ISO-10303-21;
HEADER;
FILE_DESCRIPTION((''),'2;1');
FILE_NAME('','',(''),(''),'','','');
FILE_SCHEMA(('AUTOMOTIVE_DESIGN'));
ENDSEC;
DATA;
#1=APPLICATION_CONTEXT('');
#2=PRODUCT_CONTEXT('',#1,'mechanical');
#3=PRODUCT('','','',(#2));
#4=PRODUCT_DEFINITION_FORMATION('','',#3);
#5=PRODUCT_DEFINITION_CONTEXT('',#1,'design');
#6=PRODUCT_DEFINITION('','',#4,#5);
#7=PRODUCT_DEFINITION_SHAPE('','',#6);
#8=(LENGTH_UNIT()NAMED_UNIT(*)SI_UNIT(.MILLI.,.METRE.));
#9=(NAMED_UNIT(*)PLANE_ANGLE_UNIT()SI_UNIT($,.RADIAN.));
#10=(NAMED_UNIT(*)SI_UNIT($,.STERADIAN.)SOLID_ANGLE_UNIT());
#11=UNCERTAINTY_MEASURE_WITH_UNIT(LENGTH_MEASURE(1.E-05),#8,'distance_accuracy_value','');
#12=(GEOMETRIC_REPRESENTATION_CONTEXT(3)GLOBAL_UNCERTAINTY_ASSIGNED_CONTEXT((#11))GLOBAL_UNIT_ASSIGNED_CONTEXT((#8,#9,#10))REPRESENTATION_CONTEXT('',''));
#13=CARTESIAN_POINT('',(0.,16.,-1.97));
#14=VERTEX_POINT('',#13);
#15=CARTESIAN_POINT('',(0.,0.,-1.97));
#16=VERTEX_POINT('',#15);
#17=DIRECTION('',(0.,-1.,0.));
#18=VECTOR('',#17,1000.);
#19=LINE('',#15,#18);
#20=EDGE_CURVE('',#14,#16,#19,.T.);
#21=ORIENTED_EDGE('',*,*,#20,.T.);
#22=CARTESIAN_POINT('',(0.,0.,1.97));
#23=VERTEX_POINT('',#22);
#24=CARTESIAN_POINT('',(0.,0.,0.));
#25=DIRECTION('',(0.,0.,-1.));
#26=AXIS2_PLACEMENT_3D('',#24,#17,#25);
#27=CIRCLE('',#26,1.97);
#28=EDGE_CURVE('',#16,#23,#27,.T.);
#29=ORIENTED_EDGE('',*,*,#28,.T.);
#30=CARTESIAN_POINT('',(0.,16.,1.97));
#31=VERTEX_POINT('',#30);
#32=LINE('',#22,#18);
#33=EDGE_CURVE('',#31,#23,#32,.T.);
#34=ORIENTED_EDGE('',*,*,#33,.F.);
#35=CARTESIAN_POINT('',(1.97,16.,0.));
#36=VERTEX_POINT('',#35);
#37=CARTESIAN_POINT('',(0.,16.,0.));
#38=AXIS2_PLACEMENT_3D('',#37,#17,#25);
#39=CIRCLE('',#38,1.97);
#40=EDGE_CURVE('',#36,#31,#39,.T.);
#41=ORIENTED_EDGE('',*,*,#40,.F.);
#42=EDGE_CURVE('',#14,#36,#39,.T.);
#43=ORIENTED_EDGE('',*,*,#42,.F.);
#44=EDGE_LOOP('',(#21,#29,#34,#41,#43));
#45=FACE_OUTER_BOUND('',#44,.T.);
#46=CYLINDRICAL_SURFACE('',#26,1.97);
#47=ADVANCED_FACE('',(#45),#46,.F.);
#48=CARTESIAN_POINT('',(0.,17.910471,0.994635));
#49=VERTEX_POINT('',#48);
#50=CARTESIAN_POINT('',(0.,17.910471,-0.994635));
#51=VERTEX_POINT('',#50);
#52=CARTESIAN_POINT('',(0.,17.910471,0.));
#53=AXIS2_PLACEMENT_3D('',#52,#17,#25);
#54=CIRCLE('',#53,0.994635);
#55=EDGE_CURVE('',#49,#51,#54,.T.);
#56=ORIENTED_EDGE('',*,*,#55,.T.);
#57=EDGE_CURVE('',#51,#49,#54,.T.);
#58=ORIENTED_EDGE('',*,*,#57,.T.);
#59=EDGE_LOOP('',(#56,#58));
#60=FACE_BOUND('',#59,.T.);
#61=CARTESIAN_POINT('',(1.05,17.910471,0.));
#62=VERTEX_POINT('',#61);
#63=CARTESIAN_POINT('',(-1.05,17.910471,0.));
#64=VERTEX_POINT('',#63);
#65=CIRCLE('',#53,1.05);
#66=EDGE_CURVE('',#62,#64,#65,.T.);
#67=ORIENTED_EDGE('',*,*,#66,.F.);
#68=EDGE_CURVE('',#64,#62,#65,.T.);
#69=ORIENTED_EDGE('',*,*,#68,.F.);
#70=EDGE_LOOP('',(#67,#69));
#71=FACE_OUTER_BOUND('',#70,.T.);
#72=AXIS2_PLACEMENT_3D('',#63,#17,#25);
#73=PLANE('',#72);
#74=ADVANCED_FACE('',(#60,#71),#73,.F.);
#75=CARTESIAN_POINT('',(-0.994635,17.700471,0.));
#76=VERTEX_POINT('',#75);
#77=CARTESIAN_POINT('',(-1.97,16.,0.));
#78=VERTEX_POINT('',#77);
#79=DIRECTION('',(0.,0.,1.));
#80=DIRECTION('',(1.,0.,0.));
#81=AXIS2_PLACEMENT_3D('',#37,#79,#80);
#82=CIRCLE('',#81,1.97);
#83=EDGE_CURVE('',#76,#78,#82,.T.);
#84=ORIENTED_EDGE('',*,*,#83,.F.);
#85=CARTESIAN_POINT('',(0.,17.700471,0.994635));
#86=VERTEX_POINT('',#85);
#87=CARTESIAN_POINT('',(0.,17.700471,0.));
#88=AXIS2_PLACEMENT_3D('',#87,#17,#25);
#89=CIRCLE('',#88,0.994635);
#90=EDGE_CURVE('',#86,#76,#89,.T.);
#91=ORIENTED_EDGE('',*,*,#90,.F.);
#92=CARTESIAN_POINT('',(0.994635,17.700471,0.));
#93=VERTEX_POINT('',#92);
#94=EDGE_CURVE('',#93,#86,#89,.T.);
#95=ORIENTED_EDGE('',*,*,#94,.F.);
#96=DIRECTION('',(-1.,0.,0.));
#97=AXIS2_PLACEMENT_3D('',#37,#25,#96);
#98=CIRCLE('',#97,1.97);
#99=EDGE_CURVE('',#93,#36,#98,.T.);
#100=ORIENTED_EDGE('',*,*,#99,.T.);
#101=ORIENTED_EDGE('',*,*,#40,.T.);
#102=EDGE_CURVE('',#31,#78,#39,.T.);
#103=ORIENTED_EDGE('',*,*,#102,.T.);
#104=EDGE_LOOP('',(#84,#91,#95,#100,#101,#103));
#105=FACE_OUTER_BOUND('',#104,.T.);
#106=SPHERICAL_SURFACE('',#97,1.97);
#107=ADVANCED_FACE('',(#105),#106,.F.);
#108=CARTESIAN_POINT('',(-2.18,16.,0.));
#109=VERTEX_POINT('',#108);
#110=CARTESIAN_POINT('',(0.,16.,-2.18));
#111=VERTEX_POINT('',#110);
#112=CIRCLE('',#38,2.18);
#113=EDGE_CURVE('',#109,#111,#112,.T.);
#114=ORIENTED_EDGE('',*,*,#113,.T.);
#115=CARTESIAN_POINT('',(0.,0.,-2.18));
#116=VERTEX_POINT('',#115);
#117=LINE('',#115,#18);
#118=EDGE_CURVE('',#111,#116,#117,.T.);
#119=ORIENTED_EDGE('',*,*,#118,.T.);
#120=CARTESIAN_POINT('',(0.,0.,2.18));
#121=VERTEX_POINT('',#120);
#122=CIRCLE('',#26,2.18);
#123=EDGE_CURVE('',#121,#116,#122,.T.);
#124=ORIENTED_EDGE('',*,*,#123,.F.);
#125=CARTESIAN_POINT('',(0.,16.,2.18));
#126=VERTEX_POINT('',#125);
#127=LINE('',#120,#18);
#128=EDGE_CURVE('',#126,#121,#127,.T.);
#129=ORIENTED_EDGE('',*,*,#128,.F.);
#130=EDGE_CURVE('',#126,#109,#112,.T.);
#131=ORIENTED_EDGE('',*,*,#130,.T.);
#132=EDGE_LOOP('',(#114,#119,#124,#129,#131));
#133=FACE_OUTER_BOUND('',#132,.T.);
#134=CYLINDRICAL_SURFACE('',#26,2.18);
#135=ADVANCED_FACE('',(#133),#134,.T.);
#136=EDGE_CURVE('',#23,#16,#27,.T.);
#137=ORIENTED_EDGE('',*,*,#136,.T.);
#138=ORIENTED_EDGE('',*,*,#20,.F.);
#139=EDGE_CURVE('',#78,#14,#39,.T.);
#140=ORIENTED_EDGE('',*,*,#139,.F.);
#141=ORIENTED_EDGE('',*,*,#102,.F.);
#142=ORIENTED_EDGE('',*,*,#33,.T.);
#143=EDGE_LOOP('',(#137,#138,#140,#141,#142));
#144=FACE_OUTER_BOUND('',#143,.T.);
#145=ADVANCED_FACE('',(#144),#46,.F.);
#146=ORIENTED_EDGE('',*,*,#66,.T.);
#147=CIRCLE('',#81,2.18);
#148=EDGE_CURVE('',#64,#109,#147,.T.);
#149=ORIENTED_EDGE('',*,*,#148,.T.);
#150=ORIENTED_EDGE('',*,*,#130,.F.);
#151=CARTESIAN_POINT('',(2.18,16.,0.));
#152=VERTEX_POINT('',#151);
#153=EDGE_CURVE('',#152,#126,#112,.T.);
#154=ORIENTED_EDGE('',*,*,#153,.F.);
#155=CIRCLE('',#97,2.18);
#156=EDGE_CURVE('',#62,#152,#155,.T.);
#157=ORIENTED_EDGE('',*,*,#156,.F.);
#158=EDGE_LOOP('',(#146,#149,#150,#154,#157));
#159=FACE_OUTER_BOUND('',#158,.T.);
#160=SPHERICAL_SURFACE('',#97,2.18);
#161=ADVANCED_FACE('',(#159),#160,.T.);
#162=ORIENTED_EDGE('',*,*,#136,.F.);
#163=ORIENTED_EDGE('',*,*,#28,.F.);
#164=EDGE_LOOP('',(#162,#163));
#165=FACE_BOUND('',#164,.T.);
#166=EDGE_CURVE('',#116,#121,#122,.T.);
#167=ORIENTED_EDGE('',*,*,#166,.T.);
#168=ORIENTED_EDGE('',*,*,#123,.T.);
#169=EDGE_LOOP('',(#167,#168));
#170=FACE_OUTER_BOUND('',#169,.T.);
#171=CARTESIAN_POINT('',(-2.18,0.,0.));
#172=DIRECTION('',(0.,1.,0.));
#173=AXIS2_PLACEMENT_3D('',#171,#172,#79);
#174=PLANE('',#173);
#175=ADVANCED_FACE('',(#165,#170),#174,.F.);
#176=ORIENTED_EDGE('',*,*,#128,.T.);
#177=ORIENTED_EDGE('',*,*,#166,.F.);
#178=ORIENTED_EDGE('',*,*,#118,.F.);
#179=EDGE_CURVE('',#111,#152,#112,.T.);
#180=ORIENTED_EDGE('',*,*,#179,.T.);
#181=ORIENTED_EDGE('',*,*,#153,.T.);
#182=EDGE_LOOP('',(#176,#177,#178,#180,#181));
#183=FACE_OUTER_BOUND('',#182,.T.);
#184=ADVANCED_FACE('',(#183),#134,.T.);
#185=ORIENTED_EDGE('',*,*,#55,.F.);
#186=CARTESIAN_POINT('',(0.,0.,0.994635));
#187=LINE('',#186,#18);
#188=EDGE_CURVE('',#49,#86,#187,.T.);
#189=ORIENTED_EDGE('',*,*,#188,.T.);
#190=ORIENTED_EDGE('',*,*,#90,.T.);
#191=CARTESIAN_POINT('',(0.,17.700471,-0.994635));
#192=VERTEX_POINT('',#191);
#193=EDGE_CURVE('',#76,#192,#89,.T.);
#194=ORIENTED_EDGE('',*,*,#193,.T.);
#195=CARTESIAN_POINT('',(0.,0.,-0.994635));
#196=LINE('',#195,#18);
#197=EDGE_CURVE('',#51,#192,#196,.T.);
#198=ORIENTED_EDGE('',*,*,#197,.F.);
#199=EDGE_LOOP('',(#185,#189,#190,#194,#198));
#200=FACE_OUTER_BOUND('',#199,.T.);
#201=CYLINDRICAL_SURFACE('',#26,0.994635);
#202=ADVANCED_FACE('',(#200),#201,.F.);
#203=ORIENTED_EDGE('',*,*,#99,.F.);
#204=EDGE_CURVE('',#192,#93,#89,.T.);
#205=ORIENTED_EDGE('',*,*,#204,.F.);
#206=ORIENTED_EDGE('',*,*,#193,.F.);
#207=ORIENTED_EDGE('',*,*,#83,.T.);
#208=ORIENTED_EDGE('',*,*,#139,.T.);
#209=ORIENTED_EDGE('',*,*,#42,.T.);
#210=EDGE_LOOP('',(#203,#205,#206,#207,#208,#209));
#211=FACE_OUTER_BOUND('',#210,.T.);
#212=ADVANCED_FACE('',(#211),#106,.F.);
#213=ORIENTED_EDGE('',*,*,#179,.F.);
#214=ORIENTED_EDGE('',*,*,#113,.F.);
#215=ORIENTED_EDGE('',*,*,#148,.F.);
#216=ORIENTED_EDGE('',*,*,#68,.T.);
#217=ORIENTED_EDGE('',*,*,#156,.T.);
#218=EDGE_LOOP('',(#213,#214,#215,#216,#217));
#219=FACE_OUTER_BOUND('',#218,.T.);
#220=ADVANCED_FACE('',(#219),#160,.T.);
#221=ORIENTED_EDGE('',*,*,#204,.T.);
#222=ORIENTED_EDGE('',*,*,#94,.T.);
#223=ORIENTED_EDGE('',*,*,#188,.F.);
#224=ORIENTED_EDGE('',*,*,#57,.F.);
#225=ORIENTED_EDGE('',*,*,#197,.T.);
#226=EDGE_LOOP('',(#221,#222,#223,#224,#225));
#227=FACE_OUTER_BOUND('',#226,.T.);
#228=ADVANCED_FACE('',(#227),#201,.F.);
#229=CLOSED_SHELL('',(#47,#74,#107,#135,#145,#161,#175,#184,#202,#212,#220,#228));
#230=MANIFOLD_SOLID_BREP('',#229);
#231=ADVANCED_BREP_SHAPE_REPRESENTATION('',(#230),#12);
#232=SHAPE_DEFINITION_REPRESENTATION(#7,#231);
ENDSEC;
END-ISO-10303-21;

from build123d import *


with BuildPart() as part:
    # Sketch1 → Revolve1 (revolve)
    with BuildSketch(Plane.XY, mode=Mode.PRIVATE) as revolve1_sk:
        with BuildLine():
            Line((-2.18, 0), (-2.18, 16))
            ThreePointArc((-2.18, 16), (-1.876352845, 17.109819805), (-1.05, 17.910471146))
            Line((-1.05, 17.910471146), (-0.994634547, 17.910471146))
            Line((-0.994634547, 17.910471146), (-0.994634547, 17.700471146))
            ThreePointArc((-0.994634547, 17.700471146), (-1.708849036, 16.980170889), (-1.97, 16))
            Line((-1.97, 16), (-1.97, 0))
            Line((-1.97, 0), (-2.18, 0))
        make_face()
    revolve(revolve1_sk.sketch.rotate(Axis((0, 0, 0), (0, 1, 0)), 270), axis=Axis((0, 0, 0), (0, 1, 0)))


solid = part.part
